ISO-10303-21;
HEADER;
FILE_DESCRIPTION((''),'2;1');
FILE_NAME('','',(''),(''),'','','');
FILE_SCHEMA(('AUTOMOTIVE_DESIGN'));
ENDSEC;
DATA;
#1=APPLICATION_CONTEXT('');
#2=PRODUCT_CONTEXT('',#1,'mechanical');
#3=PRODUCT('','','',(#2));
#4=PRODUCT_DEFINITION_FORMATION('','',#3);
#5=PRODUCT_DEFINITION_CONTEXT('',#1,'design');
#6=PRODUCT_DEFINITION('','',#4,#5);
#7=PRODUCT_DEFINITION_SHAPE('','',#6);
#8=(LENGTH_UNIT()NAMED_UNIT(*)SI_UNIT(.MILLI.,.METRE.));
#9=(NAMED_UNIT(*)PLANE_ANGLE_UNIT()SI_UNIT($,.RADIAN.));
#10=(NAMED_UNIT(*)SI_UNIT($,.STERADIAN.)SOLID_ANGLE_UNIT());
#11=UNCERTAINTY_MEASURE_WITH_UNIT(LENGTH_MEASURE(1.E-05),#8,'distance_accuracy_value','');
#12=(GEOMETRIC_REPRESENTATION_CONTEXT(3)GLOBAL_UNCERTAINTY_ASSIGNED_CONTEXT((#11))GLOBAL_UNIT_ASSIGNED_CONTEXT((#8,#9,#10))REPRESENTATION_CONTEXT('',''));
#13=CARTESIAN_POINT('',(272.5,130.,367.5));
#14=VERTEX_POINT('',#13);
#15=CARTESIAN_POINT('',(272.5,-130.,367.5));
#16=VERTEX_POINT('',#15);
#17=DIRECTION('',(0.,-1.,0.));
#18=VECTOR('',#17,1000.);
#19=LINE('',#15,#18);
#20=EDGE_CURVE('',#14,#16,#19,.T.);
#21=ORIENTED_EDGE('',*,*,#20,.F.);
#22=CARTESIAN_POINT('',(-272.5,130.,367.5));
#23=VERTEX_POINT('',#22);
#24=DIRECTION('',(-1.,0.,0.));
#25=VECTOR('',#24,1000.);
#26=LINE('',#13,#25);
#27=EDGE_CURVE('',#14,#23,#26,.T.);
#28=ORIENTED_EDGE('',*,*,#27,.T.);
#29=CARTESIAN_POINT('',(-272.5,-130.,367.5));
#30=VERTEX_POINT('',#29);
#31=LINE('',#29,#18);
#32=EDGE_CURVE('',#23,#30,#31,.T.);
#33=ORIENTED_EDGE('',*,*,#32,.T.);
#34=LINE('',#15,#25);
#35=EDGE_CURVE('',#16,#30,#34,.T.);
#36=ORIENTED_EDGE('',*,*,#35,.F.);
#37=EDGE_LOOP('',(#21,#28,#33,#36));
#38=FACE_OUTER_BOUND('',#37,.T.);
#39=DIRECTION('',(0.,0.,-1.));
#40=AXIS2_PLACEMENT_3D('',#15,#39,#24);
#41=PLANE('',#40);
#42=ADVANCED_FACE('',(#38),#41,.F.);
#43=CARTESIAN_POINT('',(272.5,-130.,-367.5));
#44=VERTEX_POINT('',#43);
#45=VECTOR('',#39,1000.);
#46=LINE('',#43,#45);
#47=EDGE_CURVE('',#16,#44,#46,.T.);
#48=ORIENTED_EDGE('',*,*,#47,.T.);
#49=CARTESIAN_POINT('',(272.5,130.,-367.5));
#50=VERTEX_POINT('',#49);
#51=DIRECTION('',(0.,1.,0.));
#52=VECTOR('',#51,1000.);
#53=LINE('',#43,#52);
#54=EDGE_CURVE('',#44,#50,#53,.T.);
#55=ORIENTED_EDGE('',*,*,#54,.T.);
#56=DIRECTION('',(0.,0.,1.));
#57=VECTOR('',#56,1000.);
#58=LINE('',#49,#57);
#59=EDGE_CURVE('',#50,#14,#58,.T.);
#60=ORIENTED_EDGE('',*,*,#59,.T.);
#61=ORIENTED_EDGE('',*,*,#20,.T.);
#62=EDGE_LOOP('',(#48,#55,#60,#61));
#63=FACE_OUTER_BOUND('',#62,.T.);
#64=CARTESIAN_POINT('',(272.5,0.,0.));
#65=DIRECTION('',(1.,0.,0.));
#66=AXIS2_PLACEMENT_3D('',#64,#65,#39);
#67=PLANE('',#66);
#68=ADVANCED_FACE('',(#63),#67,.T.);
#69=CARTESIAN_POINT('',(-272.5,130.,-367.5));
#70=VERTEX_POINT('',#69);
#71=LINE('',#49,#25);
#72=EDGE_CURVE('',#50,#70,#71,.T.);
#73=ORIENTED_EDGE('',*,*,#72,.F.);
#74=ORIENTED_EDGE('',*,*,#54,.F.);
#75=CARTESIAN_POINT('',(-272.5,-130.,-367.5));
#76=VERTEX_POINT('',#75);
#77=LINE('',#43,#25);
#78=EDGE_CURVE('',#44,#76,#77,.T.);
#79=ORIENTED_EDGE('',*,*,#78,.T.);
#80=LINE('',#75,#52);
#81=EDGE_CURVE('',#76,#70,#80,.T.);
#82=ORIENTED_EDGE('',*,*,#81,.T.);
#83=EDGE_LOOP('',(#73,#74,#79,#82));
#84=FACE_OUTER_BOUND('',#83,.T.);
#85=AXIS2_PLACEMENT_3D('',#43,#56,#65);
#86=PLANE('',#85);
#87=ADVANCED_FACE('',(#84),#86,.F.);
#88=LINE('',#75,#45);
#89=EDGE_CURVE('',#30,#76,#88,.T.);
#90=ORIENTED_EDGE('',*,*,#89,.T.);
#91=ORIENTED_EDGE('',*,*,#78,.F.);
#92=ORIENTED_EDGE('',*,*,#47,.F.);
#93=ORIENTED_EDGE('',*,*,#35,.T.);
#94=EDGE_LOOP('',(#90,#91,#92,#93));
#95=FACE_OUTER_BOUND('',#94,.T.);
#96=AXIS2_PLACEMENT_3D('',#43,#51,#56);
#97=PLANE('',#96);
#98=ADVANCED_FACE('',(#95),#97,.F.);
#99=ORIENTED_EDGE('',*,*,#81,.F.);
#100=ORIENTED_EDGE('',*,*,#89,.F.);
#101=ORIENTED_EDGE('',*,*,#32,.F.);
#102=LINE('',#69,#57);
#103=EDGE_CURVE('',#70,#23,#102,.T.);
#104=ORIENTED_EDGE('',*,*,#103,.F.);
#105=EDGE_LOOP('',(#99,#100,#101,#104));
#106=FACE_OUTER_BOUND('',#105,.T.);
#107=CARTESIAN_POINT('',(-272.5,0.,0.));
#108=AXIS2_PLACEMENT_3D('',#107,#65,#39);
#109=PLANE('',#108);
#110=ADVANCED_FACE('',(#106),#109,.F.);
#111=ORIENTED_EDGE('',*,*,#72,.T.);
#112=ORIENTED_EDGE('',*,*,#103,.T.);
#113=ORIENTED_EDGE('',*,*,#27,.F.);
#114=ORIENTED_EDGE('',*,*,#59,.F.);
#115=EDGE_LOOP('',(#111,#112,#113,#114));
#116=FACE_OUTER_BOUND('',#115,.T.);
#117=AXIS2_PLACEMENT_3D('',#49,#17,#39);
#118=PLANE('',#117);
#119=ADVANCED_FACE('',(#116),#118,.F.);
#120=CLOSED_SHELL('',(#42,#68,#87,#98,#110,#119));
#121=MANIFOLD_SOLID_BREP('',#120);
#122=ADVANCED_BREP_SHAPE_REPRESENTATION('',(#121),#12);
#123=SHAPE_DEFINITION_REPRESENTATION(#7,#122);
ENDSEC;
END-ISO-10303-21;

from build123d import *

# Parameters (mm, degrees)
SKETCH_1_W      = 735
SKETCH_1_H      = 260
EXTRUDE_1_DEPTH = 272.5


with BuildPart() as part:
    # 草图1 → 凸台-拉伸1 (new, symmetric)
    with BuildSketch(Plane(origin=(0, 0, 0), x_dir=(0, 0, -1), z_dir=(1, 0, 0))):
        Rectangle(SKETCH_1_W, SKETCH_1_H)
    extrude(amount=EXTRUDE_1_DEPTH, both=True)


solid = part.part
